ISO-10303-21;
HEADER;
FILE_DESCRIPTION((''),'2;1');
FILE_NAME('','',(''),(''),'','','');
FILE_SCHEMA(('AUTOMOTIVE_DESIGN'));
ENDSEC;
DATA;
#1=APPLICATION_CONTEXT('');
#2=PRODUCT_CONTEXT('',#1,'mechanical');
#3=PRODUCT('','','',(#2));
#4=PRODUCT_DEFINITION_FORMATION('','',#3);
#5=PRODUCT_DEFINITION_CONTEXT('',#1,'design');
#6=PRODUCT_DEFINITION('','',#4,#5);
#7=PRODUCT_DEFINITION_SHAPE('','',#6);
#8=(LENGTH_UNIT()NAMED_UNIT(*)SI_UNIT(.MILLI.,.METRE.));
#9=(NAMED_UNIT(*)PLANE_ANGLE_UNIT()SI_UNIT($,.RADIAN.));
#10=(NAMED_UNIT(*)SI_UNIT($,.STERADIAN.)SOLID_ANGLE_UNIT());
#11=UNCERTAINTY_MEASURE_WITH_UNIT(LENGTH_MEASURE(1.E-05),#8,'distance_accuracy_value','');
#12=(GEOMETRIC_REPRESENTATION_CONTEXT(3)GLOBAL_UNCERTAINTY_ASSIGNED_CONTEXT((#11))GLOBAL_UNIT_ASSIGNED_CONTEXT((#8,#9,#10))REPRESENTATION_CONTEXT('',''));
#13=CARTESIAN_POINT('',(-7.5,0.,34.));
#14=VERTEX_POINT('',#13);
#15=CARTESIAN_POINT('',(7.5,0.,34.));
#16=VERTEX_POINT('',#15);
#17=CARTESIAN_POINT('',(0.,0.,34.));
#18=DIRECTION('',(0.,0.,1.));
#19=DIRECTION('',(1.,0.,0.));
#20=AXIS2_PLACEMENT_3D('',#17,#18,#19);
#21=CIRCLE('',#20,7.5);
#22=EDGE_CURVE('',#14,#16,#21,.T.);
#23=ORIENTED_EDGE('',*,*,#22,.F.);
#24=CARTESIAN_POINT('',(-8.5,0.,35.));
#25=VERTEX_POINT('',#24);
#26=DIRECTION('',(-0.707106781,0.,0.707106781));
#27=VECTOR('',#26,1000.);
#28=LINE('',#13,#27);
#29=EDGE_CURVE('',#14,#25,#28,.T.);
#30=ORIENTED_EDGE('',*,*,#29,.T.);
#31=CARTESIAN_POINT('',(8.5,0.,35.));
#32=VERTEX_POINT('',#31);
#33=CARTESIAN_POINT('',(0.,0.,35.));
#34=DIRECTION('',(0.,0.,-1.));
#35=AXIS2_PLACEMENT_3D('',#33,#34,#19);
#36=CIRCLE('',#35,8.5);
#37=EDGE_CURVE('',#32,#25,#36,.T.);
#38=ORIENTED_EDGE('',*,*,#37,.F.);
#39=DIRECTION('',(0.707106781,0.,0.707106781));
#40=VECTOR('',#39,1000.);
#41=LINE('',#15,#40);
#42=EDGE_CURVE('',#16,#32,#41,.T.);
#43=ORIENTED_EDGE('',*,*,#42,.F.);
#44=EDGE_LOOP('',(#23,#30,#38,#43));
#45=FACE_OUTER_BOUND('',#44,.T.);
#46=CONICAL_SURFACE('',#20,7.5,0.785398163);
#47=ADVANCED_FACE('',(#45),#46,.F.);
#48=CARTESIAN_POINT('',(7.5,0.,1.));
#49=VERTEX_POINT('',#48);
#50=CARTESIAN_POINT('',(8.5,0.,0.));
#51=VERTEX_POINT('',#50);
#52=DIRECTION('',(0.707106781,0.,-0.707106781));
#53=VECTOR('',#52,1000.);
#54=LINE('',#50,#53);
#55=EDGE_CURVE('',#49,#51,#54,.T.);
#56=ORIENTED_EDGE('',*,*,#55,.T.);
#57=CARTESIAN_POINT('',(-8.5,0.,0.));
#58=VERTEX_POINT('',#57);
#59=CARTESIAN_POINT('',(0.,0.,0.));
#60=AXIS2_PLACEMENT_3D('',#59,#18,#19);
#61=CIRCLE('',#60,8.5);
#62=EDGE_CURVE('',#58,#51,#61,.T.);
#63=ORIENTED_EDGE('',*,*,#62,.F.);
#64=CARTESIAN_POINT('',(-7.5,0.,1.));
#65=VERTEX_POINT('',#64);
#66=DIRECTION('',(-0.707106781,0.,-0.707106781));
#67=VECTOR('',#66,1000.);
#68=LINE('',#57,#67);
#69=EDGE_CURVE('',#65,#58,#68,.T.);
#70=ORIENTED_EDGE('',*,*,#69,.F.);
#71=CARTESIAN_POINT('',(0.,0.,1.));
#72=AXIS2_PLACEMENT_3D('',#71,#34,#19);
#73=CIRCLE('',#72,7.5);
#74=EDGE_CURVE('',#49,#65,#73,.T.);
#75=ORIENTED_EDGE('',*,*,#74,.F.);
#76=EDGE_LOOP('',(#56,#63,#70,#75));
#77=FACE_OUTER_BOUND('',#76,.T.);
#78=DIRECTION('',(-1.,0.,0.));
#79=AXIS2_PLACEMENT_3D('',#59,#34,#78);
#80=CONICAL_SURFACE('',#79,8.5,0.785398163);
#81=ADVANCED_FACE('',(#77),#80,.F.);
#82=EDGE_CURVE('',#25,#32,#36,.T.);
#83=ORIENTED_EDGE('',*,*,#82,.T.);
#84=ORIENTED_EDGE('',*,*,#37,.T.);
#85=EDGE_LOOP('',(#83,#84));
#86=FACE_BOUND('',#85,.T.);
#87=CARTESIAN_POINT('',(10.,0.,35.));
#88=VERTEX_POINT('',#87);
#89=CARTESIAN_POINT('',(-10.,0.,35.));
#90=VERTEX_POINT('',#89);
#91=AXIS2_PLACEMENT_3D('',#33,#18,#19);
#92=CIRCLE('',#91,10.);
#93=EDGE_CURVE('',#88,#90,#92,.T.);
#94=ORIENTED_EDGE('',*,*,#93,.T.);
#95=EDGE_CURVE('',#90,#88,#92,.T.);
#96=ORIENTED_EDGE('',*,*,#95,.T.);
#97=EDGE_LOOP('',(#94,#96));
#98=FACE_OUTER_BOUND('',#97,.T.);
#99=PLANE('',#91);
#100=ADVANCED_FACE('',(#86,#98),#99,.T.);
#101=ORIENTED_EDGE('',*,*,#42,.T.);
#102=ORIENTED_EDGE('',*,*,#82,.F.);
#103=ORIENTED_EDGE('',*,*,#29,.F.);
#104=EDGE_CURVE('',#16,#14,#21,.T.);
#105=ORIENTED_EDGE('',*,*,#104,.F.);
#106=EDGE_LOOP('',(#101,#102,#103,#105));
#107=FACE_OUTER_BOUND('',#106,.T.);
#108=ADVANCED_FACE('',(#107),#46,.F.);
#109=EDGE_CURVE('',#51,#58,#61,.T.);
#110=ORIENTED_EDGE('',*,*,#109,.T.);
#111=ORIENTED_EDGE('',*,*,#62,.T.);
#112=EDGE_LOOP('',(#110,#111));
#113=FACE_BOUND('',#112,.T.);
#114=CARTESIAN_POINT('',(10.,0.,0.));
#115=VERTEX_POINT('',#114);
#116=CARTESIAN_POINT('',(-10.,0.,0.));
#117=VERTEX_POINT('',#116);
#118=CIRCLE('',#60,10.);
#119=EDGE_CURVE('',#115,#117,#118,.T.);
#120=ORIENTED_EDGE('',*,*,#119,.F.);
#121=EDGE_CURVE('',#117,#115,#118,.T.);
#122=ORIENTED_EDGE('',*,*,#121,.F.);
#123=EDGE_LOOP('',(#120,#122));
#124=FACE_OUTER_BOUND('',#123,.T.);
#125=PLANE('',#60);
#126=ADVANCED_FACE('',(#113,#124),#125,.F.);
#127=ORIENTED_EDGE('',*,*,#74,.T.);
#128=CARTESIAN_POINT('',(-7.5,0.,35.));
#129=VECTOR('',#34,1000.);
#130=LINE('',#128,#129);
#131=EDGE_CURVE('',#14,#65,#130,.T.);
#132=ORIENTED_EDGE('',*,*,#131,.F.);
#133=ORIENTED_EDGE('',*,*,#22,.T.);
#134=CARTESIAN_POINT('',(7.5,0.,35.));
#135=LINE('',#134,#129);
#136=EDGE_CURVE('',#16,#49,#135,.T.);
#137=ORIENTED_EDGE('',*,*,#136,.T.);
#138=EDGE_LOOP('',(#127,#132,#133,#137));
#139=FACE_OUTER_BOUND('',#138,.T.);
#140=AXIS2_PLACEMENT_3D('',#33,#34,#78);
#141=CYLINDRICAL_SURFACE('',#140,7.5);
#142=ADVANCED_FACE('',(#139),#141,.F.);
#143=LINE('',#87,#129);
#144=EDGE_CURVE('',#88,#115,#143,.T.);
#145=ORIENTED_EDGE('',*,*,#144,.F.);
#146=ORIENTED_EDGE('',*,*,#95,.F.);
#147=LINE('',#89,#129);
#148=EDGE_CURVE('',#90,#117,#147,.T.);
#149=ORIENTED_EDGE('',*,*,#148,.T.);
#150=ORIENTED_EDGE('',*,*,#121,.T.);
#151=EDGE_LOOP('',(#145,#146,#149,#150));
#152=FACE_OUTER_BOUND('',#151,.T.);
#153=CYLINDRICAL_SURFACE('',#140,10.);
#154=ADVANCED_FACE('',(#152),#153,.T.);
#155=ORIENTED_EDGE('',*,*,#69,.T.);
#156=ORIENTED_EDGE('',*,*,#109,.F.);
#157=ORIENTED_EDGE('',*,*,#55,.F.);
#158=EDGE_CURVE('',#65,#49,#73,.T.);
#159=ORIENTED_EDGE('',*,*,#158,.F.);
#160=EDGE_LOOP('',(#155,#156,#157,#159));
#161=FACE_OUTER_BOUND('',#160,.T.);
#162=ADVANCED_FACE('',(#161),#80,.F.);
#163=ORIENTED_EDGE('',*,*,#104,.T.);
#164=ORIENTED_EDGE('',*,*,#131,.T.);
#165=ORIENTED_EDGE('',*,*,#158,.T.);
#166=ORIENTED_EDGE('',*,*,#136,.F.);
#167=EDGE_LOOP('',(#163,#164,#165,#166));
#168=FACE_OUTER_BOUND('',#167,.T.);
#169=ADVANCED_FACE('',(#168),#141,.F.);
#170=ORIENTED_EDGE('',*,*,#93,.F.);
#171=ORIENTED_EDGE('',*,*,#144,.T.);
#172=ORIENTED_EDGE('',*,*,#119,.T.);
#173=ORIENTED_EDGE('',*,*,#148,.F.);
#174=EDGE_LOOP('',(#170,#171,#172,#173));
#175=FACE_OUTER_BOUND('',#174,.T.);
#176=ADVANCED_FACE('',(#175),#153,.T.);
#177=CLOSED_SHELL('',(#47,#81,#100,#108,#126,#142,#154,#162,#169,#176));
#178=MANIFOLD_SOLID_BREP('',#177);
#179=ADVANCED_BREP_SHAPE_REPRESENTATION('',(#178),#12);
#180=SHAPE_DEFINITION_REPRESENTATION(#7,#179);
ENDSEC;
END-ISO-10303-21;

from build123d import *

# Parameters (mm, degrees)
SKETCH1_R           = 10
SKETCH1_R_2         = 7.5
BOSS_EXTRUDE1_DEPTH = 35
CHAMFER1_SIZE       = 1


with BuildPart() as part:
    # Sketch1 → Boss-Extrude1 (new body)
    with BuildSketch(Plane.XY):
        Circle(SKETCH1_R)
        Circle(SKETCH1_R_2, mode=Mode.SUBTRACT)
    extrude(amount=BOSS_EXTRUDE1_DEPTH)

    # Chamfer1
    chamfer1_edges = [part.edges().sort_by_distance(p)[0] for p in [
        (-7.5, 0, 0),
        (-7.5, 0, 35),
    ]]
    chamfer(chamfer1_edges, length=CHAMFER1_SIZE)


solid = part.part
